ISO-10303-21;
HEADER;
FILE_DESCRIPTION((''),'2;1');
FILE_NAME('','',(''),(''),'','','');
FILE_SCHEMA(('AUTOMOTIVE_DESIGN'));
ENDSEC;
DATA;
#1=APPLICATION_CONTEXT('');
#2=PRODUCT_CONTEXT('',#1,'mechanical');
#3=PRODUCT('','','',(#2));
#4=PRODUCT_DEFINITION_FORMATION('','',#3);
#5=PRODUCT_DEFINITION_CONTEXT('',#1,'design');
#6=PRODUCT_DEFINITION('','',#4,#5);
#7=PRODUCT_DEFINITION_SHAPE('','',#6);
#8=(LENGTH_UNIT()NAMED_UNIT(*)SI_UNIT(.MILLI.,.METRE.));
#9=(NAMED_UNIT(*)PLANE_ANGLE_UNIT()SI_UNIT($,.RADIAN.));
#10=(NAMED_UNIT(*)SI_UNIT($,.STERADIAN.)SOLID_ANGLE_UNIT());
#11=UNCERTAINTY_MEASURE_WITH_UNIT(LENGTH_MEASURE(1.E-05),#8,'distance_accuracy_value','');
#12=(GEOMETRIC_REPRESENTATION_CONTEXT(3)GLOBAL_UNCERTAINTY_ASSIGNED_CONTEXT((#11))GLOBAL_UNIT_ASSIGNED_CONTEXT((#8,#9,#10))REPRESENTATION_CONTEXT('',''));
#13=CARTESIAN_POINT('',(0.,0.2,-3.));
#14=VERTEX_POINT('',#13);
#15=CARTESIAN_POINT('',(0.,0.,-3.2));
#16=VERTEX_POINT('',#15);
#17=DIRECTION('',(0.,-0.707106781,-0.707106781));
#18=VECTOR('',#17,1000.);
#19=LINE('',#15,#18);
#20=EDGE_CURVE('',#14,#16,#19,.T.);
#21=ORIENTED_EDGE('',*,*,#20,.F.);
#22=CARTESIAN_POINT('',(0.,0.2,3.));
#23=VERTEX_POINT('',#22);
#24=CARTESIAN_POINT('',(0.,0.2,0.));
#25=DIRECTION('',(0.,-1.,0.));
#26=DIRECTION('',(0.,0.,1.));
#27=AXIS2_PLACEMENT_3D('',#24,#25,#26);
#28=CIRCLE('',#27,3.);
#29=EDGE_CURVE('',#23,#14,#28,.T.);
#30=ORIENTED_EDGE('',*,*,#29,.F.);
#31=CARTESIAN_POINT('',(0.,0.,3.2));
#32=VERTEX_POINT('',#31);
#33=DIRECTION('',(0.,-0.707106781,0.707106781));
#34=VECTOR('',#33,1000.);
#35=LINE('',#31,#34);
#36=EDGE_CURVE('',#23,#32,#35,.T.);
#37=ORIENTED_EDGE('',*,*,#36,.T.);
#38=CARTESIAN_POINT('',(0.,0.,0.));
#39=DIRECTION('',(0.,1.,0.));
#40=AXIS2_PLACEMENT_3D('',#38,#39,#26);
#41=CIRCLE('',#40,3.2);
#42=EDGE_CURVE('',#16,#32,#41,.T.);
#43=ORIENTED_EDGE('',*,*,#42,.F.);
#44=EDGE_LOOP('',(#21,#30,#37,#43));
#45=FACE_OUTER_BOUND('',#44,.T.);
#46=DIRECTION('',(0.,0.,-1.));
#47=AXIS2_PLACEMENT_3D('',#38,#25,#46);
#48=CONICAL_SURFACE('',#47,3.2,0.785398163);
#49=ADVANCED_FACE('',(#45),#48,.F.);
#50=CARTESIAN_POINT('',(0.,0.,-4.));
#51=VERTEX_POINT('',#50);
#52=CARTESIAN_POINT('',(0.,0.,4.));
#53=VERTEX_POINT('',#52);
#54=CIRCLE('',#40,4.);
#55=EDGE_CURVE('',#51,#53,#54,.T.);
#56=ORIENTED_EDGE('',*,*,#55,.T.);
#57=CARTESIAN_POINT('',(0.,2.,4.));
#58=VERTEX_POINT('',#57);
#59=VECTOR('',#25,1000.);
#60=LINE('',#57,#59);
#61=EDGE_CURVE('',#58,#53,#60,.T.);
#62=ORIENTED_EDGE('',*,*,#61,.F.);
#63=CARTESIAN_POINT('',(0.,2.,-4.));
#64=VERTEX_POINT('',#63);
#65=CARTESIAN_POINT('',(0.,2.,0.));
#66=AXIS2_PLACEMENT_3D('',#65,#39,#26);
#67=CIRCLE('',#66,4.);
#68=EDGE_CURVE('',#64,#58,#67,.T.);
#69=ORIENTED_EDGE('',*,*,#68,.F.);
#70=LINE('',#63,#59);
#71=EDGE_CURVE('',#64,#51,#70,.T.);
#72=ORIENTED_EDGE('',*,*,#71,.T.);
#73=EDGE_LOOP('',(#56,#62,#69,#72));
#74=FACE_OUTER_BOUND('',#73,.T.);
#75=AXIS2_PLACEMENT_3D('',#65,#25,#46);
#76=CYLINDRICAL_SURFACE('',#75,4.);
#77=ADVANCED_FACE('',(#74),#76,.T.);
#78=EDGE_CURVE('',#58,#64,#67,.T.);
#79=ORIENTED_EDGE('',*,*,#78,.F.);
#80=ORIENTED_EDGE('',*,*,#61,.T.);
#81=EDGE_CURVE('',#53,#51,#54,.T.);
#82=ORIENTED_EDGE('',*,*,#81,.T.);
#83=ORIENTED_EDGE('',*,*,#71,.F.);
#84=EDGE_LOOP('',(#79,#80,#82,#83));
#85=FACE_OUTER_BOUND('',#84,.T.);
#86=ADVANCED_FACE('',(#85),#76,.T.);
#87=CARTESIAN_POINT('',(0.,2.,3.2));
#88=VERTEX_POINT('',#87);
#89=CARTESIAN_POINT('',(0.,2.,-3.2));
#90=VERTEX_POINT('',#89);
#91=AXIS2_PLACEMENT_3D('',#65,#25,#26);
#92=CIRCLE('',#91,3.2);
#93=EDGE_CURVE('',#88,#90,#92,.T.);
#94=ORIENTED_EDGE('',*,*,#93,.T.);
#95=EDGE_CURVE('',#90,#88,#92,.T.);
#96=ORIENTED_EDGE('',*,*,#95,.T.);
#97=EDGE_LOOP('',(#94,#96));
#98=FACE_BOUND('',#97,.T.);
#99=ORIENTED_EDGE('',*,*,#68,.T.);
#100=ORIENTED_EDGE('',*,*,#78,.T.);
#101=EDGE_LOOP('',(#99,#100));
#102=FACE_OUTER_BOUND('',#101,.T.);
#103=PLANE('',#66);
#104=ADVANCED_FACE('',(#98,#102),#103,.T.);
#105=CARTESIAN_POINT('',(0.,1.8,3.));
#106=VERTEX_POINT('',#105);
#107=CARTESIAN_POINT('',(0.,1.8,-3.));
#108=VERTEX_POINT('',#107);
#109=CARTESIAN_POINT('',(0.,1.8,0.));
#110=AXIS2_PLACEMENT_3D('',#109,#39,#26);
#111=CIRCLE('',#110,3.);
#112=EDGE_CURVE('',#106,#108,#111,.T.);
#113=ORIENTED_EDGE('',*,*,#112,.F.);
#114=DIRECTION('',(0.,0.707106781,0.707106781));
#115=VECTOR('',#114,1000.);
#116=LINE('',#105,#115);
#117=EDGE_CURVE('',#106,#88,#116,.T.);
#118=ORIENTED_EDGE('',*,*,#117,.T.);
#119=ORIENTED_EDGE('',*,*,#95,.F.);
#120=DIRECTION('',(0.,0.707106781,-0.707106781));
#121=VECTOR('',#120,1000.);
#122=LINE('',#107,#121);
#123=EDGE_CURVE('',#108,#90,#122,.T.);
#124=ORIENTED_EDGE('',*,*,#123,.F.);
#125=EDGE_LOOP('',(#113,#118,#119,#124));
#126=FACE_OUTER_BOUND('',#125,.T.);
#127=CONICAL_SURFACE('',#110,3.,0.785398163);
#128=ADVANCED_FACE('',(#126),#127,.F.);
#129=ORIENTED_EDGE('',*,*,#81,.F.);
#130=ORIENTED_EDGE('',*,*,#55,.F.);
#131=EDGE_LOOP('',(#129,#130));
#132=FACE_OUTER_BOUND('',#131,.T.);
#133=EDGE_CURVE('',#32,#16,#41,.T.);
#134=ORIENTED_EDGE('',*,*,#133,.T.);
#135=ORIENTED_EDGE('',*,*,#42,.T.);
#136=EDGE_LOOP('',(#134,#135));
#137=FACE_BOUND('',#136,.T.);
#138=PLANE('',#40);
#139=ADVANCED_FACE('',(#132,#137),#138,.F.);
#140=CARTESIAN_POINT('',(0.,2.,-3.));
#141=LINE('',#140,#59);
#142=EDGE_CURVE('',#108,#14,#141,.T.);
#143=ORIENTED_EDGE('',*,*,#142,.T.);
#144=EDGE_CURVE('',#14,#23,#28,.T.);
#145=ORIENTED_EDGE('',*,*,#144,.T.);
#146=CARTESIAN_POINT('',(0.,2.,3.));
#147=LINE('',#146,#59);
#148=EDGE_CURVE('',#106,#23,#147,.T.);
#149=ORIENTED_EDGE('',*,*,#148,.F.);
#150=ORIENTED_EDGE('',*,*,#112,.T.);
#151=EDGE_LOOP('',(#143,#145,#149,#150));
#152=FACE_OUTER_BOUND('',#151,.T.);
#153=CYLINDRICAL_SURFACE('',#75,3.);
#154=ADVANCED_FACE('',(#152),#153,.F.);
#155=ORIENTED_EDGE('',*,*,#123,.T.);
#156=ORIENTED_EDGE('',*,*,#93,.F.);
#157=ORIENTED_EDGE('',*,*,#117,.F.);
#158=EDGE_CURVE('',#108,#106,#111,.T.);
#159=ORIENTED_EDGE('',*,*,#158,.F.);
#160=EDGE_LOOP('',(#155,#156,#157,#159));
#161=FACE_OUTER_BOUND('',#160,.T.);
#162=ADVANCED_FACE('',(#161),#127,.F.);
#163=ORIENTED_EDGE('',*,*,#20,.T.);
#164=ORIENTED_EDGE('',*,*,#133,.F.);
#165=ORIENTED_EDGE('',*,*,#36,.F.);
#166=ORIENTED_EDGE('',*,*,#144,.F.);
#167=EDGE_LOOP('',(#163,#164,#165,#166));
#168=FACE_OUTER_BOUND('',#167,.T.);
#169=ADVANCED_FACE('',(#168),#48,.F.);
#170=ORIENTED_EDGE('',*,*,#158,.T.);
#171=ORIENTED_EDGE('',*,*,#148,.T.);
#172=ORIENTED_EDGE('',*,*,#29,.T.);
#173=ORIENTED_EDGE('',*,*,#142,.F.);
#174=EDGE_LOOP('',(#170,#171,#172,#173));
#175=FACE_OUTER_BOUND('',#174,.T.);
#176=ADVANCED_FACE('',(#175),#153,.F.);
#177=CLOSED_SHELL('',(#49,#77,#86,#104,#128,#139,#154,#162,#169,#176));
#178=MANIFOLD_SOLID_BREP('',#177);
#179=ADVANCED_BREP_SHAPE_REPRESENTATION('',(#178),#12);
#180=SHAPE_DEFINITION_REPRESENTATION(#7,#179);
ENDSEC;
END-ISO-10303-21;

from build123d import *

# Parameters (mm, degrees)
SKETCH_1_R          = 4
SKETCH_1_R_2        = 3
EXTRUDE_1_DEPTH     = 2
CHAMFER_C0_2_1_SIZE = 0.2


with BuildPart() as part:
    # 草图1 → 凸台-拉伸1 (new body)
    with BuildSketch(Plane(origin=(0, 0, 0), x_dir=(1, 0, 0), z_dir=(0, 1, 0))):
        with Locations(Location((0, 0, 0), (0, 0, 270))):
            Circle(SKETCH_1_R)
        with Locations(Location((0, 0, 0), (0, 0, 270))):
            Circle(SKETCH_1_R_2, mode=Mode.SUBTRACT)
    extrude(amount=EXTRUDE_1_DEPTH)

    # C0.2 倒角1
    chamfer_c0_2_1_edges = [part.edges().sort_by_distance(p)[0] for p in [
        (0, 0, -3),
        (0, 2, -3),
    ]]
    chamfer(chamfer_c0_2_1_edges, length=CHAMFER_C0_2_1_SIZE)


solid = part.part
